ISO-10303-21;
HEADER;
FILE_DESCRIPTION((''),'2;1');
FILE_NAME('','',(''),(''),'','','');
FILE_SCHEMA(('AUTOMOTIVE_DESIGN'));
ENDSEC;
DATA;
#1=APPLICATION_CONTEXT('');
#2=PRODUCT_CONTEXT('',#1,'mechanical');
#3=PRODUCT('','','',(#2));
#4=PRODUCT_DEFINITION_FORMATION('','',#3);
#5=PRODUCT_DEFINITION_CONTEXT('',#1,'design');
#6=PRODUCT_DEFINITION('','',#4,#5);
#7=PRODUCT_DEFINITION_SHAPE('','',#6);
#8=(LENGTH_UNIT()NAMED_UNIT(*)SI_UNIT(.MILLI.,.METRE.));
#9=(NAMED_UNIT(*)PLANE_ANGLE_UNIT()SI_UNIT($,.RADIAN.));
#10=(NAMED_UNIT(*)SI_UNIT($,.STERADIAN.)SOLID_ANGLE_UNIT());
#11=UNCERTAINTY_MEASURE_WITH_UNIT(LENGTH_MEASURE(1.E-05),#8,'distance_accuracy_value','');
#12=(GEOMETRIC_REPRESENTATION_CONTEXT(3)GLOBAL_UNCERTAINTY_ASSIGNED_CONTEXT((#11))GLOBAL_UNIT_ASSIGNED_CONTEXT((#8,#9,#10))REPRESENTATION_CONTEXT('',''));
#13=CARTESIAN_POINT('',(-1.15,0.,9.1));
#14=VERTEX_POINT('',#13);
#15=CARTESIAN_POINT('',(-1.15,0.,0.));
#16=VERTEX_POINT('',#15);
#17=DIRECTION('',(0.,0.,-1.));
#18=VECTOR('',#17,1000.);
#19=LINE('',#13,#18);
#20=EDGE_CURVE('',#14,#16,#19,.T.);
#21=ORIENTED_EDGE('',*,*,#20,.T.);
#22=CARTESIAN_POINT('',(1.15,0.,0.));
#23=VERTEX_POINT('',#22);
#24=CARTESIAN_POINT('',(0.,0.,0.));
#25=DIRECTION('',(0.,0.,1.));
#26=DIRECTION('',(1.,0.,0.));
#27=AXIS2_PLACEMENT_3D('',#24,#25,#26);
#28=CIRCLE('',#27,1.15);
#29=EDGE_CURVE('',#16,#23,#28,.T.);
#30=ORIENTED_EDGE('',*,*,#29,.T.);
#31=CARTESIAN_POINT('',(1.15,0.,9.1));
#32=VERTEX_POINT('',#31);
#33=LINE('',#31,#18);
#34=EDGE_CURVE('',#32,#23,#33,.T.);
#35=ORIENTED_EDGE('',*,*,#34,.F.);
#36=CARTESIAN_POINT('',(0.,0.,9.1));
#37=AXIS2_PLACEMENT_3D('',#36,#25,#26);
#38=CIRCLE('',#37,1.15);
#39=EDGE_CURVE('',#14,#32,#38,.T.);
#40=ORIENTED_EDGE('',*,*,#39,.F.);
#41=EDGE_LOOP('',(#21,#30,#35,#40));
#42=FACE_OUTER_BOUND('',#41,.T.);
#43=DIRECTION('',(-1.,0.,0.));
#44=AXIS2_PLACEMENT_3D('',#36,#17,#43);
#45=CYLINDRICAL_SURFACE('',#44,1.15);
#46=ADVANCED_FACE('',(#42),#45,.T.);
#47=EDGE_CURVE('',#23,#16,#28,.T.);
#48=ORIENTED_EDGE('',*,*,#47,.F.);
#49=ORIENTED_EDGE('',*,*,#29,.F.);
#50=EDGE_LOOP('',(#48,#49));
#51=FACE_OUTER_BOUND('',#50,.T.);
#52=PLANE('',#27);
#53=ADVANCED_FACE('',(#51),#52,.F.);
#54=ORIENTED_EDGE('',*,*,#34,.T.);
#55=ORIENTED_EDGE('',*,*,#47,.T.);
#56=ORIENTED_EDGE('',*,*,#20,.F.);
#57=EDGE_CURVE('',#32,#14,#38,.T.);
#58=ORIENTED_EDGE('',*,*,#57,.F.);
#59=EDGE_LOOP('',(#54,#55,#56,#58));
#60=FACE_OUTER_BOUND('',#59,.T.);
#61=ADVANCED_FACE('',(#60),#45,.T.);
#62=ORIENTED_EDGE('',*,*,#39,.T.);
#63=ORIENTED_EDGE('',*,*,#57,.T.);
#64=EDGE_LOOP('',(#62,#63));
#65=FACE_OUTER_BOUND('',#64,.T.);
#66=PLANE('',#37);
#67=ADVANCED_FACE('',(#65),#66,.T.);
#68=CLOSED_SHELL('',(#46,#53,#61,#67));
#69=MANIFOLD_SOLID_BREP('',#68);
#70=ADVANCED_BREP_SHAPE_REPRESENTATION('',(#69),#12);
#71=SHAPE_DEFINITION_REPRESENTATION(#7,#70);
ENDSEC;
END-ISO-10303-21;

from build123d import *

# Parameters (mm, degrees)
SKETCH_1_R      = 1.15
EXTRUDE_1_DEPTH = 9.1


with BuildPart() as part:
    # 草图1 → 凸台-拉伸1 (new body)
    with BuildSketch(Plane.XY):
        Circle(SKETCH_1_R)
    extrude(amount=EXTRUDE_1_DEPTH)


solid = part.part
